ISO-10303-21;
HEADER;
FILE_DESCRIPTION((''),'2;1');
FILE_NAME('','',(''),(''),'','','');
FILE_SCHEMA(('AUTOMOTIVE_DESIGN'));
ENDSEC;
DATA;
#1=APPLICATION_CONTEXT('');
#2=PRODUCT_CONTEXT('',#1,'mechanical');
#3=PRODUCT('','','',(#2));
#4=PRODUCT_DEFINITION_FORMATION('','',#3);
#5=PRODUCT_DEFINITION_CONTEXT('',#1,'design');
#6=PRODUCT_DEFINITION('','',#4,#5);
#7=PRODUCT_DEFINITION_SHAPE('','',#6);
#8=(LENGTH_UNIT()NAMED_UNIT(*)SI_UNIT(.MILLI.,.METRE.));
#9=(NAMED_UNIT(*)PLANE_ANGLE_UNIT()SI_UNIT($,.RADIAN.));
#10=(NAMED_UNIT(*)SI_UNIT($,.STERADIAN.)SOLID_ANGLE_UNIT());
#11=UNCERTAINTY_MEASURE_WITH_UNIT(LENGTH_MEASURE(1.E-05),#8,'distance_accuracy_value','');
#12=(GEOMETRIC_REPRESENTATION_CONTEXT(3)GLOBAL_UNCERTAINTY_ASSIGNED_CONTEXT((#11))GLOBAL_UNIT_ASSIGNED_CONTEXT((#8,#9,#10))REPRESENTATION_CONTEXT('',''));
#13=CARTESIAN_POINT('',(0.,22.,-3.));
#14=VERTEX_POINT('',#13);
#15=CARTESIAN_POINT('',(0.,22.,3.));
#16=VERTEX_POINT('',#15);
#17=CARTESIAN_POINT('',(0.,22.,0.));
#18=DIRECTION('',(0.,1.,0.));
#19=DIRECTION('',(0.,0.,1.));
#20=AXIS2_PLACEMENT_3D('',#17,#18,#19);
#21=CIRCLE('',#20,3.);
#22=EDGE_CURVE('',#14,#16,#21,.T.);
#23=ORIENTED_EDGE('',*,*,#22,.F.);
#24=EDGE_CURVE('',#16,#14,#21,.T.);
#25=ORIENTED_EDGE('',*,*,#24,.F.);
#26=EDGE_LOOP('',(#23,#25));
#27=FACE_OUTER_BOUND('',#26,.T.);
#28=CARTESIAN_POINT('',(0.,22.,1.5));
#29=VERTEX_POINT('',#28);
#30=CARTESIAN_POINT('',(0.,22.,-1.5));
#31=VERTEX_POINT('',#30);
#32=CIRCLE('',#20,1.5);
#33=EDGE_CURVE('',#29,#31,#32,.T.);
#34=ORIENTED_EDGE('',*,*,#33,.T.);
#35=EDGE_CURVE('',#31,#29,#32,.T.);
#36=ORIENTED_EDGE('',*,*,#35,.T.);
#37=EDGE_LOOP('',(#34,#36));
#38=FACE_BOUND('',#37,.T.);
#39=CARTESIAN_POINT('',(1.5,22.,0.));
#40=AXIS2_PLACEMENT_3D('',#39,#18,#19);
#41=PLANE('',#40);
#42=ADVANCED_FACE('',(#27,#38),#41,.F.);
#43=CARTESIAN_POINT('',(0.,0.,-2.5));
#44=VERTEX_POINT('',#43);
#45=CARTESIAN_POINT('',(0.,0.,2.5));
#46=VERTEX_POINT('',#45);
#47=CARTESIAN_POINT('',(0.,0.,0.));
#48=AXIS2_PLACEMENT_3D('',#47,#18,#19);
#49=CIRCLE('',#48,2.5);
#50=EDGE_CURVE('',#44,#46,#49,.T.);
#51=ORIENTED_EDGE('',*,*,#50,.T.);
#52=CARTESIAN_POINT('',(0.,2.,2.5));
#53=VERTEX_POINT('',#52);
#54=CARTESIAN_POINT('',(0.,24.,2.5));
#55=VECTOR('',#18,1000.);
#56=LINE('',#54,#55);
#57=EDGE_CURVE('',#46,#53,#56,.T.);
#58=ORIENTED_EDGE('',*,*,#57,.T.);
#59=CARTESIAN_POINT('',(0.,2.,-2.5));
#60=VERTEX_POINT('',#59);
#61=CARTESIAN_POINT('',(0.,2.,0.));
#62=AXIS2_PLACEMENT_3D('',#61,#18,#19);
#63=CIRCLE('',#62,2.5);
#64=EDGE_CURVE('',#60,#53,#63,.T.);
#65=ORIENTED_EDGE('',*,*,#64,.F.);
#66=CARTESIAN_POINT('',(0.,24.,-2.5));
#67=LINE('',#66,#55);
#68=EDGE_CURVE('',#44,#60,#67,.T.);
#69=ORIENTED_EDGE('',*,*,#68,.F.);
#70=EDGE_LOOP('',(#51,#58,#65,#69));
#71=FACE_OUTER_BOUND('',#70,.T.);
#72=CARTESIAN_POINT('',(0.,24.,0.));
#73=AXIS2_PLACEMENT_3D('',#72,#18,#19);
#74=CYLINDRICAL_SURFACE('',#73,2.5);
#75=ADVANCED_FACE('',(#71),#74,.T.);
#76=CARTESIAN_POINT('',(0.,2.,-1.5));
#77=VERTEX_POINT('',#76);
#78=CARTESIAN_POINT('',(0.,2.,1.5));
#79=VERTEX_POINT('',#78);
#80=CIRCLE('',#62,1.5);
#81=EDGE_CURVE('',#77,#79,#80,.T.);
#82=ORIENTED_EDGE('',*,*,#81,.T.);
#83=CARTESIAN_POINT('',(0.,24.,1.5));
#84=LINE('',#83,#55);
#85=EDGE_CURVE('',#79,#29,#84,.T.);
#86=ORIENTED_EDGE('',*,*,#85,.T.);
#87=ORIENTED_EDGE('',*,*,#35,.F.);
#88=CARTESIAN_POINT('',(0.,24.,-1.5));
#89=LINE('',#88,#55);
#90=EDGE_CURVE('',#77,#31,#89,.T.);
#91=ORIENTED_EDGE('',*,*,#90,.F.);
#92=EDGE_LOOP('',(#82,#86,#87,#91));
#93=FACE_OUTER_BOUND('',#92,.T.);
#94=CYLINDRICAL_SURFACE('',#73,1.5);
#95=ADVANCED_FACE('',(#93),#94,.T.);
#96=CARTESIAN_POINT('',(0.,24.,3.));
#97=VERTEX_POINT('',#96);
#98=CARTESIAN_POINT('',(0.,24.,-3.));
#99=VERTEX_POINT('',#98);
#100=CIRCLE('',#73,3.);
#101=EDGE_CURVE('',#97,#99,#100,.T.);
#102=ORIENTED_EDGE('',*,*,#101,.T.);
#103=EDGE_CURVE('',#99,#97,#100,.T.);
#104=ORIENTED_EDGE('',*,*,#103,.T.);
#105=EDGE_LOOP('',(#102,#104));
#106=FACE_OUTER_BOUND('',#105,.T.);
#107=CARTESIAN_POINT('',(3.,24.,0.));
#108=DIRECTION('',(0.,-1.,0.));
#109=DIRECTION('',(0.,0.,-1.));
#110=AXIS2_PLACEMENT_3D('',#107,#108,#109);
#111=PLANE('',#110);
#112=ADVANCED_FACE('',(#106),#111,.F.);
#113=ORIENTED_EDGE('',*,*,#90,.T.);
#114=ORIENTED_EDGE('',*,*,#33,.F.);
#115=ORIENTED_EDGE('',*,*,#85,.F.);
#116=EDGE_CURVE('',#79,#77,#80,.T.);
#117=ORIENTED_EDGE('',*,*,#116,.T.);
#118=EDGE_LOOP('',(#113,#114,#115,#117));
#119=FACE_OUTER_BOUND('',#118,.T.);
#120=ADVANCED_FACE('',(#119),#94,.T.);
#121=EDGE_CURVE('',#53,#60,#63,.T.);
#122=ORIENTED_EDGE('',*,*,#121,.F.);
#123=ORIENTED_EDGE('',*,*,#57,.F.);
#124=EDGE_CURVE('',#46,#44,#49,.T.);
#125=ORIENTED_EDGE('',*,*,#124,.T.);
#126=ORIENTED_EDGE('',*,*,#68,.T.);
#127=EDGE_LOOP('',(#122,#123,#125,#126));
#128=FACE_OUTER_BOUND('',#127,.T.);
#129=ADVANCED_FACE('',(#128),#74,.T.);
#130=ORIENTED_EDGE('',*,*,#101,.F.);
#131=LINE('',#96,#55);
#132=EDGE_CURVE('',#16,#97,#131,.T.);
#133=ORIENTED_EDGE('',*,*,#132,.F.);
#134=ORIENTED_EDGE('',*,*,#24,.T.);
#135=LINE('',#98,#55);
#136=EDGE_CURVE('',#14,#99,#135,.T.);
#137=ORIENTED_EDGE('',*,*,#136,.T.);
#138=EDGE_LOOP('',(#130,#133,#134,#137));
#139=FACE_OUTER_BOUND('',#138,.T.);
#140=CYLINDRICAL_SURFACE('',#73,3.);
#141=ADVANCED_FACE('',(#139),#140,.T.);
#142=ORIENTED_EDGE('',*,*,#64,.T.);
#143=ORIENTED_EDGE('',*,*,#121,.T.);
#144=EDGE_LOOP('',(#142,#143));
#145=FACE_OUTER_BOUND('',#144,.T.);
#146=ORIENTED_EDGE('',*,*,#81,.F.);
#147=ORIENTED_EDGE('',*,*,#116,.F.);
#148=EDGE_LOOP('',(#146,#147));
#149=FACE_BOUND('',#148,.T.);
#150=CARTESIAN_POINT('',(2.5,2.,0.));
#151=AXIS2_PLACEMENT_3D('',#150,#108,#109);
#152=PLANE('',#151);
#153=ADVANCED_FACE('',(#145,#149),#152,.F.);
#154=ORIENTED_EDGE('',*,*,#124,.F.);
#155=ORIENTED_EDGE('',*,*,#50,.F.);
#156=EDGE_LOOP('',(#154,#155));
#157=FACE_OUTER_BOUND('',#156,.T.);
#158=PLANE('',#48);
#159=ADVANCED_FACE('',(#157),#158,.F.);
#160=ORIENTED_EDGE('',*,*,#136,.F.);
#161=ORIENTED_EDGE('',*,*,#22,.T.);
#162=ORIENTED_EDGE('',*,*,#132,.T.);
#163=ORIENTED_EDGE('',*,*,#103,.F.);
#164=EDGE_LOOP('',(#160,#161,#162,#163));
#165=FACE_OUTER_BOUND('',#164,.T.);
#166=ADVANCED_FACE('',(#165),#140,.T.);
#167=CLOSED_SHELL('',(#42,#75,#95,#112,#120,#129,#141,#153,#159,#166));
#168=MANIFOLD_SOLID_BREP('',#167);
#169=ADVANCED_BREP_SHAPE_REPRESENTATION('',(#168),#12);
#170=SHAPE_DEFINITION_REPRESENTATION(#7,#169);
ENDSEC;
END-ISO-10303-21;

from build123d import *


with BuildPart() as part:
    # Sketch1 → Revolve1 (revolve)
    with BuildSketch(Plane.XY, mode=Mode.PRIVATE) as revolve1_sk:
        Polygon((0, 0), (2.5, 0), (2.5, 2), (1.5, 2), (1.5, 22), (3, 22), (3, 24), (0, 24), align=None)
    revolve(revolve1_sk.sketch.rotate(Axis((0, 24, 0), (0, -1, 0)), 90), axis=Axis((0, 24, 0), (0, -1, 0)))


solid = part.part
